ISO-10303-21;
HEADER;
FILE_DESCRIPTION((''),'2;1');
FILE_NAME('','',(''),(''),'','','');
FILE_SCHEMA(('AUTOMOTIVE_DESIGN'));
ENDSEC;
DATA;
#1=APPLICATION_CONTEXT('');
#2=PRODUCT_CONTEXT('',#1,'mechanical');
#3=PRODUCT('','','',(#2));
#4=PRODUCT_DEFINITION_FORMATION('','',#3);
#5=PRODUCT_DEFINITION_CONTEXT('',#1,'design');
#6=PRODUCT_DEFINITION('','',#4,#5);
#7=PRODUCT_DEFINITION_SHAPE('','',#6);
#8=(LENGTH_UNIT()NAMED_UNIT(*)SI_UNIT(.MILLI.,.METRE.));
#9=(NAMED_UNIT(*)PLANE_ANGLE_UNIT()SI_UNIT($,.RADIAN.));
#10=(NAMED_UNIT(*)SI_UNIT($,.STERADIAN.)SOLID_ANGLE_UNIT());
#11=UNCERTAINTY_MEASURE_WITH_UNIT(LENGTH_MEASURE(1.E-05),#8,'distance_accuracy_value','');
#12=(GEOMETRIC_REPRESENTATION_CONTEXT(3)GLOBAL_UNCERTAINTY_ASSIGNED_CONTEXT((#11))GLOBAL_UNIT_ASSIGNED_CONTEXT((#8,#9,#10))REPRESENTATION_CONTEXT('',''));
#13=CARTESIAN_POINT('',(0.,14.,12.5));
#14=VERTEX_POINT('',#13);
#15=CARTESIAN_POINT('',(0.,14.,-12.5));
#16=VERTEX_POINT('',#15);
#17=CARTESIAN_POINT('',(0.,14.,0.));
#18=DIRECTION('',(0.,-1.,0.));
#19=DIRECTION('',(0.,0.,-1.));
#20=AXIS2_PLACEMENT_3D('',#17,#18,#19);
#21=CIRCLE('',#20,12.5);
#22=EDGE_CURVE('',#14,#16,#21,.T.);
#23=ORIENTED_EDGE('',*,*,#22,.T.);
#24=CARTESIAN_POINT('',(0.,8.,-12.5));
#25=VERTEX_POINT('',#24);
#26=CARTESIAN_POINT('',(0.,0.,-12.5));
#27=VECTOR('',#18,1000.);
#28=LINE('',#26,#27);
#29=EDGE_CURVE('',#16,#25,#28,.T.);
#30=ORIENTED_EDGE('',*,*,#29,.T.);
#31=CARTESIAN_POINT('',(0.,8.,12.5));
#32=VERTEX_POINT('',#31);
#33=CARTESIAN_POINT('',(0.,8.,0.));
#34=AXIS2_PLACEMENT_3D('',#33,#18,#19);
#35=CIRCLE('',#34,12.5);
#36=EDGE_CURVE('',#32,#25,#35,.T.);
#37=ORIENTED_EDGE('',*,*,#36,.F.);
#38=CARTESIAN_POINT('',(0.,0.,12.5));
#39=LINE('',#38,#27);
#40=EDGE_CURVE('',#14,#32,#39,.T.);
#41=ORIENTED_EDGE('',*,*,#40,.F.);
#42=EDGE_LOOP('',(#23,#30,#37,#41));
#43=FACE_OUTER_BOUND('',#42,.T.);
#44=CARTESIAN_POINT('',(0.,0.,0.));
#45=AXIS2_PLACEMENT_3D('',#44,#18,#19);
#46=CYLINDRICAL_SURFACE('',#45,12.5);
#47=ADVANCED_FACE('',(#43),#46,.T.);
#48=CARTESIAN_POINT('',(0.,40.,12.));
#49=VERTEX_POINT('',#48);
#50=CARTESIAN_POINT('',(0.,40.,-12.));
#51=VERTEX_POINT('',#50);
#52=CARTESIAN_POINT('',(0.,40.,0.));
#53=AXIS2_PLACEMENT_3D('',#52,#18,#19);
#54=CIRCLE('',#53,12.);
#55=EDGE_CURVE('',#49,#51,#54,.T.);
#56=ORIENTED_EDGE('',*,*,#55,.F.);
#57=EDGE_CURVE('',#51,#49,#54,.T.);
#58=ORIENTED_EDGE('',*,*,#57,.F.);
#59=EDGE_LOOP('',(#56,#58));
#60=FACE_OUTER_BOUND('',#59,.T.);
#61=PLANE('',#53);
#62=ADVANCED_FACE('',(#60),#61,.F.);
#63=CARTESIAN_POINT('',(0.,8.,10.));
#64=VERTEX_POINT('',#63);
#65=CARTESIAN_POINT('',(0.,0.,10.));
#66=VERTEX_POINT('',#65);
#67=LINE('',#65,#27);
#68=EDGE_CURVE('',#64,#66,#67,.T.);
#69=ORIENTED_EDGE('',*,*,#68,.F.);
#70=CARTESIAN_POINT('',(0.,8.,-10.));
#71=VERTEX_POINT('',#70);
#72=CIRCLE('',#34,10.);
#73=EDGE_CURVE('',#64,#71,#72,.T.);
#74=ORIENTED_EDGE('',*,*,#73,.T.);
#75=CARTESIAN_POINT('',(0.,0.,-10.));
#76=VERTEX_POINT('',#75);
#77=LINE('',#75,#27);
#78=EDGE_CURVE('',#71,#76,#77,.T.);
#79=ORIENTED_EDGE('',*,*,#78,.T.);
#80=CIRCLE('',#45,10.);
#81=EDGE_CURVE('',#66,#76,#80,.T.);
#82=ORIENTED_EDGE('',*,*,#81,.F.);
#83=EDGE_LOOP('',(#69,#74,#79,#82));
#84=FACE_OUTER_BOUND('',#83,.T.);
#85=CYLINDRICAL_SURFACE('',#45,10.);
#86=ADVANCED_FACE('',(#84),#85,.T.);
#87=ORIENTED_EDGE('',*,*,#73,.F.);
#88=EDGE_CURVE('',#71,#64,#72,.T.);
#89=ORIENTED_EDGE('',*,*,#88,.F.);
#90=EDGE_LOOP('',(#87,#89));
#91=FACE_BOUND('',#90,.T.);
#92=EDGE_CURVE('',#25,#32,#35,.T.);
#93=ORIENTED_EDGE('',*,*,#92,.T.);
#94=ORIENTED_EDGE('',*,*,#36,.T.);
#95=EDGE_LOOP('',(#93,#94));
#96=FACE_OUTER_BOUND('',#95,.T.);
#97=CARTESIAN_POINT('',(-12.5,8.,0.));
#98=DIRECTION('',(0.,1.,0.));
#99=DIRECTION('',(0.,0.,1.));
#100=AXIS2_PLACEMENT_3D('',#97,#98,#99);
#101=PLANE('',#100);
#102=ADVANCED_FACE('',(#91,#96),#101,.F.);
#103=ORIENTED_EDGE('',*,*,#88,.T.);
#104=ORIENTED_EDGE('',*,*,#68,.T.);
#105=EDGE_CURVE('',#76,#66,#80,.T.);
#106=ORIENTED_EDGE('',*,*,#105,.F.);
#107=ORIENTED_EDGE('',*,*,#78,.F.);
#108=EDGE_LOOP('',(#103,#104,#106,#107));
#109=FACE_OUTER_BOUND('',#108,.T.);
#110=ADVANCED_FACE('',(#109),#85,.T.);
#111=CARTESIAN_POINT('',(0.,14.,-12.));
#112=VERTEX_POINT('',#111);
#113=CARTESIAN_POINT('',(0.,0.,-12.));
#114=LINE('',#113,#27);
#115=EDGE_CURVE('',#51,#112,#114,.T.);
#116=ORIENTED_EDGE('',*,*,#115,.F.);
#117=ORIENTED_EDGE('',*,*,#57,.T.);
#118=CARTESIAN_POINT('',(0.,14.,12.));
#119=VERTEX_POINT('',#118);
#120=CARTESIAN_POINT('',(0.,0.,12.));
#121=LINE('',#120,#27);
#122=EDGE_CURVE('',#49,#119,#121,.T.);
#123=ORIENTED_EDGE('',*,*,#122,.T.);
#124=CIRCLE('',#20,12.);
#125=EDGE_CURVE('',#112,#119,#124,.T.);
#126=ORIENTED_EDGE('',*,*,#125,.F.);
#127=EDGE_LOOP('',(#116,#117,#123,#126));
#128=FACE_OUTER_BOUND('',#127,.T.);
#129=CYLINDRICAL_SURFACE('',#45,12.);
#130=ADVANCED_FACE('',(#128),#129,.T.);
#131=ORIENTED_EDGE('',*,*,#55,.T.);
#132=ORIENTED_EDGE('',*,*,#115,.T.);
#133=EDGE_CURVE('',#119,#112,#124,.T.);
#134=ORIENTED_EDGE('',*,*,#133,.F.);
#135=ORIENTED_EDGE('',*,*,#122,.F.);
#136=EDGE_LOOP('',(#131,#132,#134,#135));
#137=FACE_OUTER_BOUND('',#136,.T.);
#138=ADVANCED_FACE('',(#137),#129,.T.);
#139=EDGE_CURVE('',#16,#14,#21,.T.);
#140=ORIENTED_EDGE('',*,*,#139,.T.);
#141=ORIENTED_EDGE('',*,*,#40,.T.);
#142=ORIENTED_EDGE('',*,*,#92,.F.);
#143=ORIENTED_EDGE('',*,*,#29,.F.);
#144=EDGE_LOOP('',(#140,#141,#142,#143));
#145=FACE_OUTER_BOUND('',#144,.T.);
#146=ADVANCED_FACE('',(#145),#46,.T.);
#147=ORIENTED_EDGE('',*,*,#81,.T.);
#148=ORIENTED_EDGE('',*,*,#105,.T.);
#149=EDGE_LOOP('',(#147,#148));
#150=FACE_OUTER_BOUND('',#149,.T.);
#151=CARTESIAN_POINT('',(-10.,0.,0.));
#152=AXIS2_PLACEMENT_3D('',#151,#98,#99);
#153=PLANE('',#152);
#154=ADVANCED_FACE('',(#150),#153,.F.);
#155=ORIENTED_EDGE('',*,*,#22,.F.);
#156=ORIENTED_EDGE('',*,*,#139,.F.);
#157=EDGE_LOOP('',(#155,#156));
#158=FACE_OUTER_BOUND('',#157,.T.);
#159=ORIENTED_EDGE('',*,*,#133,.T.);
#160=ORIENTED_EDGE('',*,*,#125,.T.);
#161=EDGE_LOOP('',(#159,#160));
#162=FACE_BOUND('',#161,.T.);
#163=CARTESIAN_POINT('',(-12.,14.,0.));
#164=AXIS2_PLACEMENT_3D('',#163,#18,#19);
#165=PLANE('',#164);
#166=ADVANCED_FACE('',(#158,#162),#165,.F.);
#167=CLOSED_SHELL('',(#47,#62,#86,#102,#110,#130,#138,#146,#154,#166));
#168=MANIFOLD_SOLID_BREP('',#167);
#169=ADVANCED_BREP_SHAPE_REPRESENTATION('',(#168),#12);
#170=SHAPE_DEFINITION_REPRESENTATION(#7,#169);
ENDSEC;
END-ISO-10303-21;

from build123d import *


with BuildPart() as part:
    # Sketch1 → Revolve1 (revolve)
    with BuildSketch(Plane.XY, mode=Mode.PRIVATE) as revolve1_sk:
        Polygon((0, 40), (-12, 40), (-12, 14), (-12.5, 14), (-12.5, 8), (-10, 8), (-10, 0), (0, 0), align=None)
    revolve(revolve1_sk.sketch.rotate(Axis((0, 0, 0), (0, 1, 0)), 270), axis=Axis((0, 0, 0), (0, 1, 0)))


solid = part.part
